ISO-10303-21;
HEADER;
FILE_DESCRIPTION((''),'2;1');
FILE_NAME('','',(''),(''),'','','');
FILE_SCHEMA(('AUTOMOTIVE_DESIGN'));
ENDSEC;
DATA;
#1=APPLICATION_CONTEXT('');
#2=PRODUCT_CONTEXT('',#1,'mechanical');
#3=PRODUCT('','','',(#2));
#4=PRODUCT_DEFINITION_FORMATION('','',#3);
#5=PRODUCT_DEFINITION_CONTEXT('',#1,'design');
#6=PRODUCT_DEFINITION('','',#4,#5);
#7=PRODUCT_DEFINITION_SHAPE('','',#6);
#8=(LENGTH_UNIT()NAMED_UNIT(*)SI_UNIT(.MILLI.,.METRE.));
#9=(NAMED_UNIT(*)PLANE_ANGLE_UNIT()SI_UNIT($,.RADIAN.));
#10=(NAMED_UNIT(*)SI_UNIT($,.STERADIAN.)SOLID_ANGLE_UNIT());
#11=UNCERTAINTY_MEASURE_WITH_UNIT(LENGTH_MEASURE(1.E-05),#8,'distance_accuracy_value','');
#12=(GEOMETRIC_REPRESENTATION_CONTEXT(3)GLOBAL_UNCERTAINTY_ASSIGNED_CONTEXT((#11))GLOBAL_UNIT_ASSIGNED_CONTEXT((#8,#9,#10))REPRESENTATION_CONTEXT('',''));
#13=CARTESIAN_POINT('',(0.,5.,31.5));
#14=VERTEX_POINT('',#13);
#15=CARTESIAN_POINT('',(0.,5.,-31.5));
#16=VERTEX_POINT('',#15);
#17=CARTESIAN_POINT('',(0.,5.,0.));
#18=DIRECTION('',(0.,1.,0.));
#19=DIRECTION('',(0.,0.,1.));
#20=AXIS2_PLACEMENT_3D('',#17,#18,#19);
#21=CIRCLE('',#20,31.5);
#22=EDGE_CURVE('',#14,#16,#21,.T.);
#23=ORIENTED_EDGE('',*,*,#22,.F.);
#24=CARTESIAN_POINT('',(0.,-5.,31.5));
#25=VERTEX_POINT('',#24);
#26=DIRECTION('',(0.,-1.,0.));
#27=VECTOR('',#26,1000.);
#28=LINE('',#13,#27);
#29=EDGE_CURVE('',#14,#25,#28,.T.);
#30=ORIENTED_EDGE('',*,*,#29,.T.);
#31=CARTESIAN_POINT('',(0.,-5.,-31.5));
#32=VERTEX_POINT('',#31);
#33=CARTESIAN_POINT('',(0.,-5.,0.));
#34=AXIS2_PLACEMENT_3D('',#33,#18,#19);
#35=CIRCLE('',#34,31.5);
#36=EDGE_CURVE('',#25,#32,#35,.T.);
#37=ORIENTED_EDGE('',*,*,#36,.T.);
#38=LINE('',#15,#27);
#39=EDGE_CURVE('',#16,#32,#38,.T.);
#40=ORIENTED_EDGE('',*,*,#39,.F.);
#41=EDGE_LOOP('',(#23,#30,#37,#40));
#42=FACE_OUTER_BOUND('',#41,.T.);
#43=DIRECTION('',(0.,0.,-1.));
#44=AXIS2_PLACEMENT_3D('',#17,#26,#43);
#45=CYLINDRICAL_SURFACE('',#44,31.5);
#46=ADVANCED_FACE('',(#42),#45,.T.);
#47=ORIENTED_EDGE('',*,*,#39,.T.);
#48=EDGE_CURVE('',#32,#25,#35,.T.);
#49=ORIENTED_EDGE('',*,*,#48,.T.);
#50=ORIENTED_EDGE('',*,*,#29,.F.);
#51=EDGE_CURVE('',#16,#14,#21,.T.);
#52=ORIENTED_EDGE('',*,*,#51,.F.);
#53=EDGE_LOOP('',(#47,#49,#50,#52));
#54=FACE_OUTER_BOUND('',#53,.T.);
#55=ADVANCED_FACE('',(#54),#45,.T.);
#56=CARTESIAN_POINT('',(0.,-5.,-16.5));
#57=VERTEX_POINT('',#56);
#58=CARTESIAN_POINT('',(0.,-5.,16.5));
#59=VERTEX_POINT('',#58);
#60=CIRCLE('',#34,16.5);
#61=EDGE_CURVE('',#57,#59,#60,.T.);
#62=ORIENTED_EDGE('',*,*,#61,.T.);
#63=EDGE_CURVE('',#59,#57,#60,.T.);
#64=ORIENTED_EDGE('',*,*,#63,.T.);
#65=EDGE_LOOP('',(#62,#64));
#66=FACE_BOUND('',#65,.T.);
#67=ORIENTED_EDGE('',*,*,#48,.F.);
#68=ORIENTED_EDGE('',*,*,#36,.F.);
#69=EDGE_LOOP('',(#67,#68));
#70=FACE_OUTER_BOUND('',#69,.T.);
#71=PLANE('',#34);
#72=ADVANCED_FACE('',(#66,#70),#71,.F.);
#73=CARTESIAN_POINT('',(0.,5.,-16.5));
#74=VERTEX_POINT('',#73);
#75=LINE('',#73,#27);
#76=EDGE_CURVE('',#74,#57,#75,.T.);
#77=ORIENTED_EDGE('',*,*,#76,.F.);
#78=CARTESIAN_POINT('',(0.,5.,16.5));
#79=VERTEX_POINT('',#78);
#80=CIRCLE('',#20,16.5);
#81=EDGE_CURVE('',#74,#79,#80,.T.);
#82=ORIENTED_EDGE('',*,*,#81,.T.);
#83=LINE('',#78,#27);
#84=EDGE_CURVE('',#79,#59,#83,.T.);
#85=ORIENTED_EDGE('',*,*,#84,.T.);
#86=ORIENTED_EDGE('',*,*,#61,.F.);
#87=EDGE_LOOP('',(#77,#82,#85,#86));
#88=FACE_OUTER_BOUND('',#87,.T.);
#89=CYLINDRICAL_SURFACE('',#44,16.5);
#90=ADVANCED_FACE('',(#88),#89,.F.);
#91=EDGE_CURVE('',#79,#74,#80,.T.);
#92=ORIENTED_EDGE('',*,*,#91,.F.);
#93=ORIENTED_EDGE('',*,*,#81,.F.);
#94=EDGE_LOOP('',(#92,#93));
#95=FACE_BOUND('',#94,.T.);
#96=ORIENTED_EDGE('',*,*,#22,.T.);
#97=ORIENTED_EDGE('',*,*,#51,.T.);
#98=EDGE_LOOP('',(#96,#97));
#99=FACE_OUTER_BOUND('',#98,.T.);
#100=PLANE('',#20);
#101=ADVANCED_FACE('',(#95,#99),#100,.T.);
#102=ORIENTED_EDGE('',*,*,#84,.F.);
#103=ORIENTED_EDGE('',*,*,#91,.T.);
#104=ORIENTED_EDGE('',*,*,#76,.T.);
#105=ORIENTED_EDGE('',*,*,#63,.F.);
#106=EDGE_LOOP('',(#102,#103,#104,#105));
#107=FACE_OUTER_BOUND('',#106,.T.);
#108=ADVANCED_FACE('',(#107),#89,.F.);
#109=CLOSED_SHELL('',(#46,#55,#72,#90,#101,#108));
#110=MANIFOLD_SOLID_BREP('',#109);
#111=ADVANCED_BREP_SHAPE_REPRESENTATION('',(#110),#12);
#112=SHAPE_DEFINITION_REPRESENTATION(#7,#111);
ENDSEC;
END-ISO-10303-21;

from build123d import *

# Parameters (mm, degrees)
WASHER_PROFILE_63_X_33_R   = 31.5
WASHER_PROFILE_63_X_33_R_2 = 16.5
WASHER_BODY_10MM_DEPTH     = 5


with BuildPart() as part:
    # Washer Profile Ø63 x Ø33 → Washer Body 10mm (new, symmetric)
    with BuildSketch(Plane(origin=(0, 0, 0), x_dir=(1, 0, 0), z_dir=(0, 1, 0))):
        with Locations(Location((0, 0, 0), (0, 0, 270))):
            Circle(WASHER_PROFILE_63_X_33_R)
        with Locations(Location((0, 0, 0), (0, 0, 270))):
            Circle(WASHER_PROFILE_63_X_33_R_2, mode=Mode.SUBTRACT)
    extrude(amount=WASHER_BODY_10MM_DEPTH, both=True)


solid = part.part
